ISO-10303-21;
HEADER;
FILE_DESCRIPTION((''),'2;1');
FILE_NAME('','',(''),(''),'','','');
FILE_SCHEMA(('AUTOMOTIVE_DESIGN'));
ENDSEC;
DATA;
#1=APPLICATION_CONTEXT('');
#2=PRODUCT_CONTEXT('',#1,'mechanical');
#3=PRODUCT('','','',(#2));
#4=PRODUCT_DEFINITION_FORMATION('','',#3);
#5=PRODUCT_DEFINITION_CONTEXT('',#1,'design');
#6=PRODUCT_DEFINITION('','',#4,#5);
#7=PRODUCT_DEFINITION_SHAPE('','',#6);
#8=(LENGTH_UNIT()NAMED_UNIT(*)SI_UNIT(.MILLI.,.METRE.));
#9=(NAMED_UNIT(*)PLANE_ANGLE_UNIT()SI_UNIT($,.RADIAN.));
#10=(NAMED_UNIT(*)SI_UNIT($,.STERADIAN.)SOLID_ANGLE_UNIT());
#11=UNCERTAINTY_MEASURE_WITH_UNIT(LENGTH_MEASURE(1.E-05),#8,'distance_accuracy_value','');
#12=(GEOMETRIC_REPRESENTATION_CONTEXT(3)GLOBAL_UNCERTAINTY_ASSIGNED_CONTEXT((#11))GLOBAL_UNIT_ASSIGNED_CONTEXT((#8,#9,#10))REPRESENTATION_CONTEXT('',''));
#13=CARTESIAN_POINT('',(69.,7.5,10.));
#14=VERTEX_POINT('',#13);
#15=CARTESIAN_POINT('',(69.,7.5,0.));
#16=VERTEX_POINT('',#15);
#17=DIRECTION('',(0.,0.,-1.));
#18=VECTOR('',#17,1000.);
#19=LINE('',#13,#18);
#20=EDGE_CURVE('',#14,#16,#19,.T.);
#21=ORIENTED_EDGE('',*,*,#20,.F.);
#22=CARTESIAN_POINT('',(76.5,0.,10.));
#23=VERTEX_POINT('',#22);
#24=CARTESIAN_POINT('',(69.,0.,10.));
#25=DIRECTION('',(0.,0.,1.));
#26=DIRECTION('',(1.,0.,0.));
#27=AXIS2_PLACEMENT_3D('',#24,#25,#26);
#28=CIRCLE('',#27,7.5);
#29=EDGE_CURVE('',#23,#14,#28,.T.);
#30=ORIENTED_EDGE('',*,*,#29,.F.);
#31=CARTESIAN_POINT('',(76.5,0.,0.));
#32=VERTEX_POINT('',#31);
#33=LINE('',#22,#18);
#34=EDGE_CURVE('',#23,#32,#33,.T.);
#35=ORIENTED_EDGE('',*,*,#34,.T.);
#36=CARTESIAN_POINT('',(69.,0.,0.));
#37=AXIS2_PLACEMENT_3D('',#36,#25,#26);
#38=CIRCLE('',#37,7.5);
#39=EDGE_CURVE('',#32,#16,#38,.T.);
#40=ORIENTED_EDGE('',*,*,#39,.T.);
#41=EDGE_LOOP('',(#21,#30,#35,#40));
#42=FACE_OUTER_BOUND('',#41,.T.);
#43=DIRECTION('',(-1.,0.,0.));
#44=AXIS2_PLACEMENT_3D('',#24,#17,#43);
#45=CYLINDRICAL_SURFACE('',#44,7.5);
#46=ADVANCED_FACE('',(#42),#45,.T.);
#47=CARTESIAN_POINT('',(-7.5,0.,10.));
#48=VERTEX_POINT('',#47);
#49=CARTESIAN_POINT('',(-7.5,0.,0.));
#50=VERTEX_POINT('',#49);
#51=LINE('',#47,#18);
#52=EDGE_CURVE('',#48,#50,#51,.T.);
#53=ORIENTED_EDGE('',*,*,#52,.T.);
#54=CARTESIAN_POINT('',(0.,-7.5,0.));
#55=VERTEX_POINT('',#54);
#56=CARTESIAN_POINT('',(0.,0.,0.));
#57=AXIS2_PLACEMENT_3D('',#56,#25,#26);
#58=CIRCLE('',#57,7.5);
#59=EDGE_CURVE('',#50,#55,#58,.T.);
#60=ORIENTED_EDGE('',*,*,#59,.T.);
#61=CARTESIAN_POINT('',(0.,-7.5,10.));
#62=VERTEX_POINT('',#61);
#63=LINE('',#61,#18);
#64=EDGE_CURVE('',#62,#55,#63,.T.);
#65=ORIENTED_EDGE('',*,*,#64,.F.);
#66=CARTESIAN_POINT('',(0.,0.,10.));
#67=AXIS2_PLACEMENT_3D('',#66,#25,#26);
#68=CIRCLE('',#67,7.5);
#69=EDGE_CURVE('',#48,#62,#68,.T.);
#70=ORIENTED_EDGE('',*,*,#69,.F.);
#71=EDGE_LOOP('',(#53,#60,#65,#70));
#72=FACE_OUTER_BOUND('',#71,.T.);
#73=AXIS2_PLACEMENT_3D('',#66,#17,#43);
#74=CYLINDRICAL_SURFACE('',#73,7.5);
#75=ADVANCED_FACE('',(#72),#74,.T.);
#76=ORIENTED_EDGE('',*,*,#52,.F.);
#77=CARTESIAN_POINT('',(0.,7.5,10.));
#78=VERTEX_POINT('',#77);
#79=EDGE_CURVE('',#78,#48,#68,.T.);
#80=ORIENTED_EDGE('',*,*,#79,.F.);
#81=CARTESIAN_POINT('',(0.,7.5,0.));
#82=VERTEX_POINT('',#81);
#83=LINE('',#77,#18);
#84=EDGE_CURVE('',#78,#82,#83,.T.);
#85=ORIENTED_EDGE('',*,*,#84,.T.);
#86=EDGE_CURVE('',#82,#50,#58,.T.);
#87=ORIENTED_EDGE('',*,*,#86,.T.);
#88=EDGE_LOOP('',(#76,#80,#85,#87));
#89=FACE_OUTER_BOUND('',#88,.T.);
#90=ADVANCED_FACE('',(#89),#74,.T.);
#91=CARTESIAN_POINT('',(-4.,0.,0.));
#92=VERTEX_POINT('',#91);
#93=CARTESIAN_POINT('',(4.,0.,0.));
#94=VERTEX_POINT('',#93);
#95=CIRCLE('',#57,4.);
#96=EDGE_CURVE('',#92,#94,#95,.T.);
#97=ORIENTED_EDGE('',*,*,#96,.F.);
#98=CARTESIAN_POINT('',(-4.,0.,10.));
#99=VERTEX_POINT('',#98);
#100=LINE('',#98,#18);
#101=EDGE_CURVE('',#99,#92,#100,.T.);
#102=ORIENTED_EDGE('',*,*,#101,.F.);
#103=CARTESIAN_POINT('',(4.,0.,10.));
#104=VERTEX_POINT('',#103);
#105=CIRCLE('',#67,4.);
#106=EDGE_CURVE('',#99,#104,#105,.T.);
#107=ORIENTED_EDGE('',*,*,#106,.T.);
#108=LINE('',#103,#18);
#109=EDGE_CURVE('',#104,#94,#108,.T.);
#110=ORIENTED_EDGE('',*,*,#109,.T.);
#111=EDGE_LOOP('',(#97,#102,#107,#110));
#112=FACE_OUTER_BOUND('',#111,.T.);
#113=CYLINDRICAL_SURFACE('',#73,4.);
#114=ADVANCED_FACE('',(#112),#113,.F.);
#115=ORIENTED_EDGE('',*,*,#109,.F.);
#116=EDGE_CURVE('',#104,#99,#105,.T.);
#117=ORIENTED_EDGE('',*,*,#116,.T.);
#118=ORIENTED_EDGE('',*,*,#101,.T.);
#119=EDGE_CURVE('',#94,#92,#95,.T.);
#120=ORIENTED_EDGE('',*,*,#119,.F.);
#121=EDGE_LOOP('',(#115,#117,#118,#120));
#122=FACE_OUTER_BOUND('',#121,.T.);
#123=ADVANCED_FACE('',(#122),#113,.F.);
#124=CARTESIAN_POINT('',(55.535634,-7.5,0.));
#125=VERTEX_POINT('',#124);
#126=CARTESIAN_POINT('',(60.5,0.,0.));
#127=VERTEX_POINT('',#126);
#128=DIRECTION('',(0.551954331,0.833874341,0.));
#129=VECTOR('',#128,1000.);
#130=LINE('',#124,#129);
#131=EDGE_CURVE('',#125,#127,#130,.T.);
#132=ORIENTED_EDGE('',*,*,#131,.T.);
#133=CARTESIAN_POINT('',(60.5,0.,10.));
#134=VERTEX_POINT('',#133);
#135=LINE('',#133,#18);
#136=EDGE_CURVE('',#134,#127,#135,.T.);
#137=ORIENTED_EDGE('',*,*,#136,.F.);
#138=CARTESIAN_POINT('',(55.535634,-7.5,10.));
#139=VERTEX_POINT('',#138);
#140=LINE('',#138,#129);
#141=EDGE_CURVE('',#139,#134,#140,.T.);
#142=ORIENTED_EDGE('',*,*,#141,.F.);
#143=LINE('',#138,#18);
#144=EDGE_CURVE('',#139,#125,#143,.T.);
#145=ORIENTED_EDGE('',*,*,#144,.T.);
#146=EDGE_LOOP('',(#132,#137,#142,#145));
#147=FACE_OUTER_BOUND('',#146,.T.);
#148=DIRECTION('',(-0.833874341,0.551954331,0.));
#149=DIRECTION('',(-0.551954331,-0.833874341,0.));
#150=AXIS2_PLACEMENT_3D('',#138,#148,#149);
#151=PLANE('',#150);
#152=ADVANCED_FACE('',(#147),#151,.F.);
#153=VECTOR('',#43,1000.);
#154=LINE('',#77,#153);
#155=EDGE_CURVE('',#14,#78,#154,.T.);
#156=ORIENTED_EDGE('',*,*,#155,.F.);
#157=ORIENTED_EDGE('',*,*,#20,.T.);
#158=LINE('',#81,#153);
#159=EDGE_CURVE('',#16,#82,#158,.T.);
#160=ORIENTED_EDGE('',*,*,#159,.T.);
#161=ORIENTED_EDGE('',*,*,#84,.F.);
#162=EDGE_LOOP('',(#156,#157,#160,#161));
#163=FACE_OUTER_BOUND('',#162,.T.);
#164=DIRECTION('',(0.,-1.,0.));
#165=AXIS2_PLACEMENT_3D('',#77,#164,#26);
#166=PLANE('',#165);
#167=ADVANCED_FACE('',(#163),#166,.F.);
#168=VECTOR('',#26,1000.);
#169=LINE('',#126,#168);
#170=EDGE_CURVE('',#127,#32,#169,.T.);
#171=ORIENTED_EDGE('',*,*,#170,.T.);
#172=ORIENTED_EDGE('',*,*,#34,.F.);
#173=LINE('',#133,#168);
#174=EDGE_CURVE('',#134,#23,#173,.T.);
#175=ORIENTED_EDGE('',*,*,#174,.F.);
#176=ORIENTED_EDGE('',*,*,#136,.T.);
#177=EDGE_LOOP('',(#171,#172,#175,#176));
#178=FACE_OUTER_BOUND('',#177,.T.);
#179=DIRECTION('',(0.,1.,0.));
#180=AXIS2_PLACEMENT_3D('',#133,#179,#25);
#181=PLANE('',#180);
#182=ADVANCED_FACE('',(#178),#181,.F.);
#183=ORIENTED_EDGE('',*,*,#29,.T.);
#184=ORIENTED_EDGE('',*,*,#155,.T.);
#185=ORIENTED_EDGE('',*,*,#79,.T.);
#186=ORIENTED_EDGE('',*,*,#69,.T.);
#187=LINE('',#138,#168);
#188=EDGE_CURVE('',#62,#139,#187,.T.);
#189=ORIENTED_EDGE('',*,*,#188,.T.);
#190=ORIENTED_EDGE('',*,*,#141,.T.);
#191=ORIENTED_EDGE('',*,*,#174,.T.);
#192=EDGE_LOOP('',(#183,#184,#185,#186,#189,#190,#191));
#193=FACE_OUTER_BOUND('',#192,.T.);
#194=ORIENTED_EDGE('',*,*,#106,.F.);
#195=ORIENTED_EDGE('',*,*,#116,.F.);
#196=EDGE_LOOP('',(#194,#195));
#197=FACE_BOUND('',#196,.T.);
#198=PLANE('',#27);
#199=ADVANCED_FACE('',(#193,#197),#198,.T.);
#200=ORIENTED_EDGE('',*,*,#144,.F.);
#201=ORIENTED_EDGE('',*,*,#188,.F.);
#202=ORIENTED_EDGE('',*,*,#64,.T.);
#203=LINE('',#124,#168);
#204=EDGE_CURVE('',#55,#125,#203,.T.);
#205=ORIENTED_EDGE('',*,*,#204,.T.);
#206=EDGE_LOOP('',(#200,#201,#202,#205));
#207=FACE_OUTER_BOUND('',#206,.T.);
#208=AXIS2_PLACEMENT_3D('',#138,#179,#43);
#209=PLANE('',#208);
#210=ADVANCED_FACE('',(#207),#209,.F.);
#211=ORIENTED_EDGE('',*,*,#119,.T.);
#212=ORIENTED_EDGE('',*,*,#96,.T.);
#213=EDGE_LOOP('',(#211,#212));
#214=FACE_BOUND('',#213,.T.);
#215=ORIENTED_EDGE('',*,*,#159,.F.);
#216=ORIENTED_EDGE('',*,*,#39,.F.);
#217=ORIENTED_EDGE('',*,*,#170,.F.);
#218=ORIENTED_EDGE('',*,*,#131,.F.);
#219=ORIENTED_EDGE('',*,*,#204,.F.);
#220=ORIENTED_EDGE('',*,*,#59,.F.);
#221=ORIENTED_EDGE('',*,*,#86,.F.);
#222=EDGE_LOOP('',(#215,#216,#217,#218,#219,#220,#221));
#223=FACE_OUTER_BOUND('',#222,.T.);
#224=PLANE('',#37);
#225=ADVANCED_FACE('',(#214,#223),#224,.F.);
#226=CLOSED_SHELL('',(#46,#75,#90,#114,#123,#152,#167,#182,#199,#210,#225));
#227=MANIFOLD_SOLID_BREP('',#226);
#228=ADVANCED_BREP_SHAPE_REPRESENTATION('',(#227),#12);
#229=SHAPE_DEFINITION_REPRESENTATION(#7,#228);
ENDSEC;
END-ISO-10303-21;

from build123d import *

# Parameters (mm, degrees)
SKETCH1_R           = 4
BOSS_EXTRUDE1_DEPTH = 10


with BuildPart() as part:
    # Sketch1 → Boss-Extrude1 (new body)
    with BuildSketch(Plane.XY):
        with BuildLine():
            Line((0, 7.5), (69, 7.5))
            ThreePointArc((69, 7.5), (74.303300859, 5.303300859), (76.5, 0))
            Line((76.5, 0), (60.5, 0))
            Line((60.5, 0), (55.535633926, -7.5))
            Line((55.535633926, -7.5), (0, -7.5))
            ThreePointArc((0, -7.5), (-7.5, 0), (0, 7.5))
        make_face()
        Circle(SKETCH1_R, mode=Mode.SUBTRACT)
    extrude(amount=BOSS_EXTRUDE1_DEPTH)


solid = part.part
